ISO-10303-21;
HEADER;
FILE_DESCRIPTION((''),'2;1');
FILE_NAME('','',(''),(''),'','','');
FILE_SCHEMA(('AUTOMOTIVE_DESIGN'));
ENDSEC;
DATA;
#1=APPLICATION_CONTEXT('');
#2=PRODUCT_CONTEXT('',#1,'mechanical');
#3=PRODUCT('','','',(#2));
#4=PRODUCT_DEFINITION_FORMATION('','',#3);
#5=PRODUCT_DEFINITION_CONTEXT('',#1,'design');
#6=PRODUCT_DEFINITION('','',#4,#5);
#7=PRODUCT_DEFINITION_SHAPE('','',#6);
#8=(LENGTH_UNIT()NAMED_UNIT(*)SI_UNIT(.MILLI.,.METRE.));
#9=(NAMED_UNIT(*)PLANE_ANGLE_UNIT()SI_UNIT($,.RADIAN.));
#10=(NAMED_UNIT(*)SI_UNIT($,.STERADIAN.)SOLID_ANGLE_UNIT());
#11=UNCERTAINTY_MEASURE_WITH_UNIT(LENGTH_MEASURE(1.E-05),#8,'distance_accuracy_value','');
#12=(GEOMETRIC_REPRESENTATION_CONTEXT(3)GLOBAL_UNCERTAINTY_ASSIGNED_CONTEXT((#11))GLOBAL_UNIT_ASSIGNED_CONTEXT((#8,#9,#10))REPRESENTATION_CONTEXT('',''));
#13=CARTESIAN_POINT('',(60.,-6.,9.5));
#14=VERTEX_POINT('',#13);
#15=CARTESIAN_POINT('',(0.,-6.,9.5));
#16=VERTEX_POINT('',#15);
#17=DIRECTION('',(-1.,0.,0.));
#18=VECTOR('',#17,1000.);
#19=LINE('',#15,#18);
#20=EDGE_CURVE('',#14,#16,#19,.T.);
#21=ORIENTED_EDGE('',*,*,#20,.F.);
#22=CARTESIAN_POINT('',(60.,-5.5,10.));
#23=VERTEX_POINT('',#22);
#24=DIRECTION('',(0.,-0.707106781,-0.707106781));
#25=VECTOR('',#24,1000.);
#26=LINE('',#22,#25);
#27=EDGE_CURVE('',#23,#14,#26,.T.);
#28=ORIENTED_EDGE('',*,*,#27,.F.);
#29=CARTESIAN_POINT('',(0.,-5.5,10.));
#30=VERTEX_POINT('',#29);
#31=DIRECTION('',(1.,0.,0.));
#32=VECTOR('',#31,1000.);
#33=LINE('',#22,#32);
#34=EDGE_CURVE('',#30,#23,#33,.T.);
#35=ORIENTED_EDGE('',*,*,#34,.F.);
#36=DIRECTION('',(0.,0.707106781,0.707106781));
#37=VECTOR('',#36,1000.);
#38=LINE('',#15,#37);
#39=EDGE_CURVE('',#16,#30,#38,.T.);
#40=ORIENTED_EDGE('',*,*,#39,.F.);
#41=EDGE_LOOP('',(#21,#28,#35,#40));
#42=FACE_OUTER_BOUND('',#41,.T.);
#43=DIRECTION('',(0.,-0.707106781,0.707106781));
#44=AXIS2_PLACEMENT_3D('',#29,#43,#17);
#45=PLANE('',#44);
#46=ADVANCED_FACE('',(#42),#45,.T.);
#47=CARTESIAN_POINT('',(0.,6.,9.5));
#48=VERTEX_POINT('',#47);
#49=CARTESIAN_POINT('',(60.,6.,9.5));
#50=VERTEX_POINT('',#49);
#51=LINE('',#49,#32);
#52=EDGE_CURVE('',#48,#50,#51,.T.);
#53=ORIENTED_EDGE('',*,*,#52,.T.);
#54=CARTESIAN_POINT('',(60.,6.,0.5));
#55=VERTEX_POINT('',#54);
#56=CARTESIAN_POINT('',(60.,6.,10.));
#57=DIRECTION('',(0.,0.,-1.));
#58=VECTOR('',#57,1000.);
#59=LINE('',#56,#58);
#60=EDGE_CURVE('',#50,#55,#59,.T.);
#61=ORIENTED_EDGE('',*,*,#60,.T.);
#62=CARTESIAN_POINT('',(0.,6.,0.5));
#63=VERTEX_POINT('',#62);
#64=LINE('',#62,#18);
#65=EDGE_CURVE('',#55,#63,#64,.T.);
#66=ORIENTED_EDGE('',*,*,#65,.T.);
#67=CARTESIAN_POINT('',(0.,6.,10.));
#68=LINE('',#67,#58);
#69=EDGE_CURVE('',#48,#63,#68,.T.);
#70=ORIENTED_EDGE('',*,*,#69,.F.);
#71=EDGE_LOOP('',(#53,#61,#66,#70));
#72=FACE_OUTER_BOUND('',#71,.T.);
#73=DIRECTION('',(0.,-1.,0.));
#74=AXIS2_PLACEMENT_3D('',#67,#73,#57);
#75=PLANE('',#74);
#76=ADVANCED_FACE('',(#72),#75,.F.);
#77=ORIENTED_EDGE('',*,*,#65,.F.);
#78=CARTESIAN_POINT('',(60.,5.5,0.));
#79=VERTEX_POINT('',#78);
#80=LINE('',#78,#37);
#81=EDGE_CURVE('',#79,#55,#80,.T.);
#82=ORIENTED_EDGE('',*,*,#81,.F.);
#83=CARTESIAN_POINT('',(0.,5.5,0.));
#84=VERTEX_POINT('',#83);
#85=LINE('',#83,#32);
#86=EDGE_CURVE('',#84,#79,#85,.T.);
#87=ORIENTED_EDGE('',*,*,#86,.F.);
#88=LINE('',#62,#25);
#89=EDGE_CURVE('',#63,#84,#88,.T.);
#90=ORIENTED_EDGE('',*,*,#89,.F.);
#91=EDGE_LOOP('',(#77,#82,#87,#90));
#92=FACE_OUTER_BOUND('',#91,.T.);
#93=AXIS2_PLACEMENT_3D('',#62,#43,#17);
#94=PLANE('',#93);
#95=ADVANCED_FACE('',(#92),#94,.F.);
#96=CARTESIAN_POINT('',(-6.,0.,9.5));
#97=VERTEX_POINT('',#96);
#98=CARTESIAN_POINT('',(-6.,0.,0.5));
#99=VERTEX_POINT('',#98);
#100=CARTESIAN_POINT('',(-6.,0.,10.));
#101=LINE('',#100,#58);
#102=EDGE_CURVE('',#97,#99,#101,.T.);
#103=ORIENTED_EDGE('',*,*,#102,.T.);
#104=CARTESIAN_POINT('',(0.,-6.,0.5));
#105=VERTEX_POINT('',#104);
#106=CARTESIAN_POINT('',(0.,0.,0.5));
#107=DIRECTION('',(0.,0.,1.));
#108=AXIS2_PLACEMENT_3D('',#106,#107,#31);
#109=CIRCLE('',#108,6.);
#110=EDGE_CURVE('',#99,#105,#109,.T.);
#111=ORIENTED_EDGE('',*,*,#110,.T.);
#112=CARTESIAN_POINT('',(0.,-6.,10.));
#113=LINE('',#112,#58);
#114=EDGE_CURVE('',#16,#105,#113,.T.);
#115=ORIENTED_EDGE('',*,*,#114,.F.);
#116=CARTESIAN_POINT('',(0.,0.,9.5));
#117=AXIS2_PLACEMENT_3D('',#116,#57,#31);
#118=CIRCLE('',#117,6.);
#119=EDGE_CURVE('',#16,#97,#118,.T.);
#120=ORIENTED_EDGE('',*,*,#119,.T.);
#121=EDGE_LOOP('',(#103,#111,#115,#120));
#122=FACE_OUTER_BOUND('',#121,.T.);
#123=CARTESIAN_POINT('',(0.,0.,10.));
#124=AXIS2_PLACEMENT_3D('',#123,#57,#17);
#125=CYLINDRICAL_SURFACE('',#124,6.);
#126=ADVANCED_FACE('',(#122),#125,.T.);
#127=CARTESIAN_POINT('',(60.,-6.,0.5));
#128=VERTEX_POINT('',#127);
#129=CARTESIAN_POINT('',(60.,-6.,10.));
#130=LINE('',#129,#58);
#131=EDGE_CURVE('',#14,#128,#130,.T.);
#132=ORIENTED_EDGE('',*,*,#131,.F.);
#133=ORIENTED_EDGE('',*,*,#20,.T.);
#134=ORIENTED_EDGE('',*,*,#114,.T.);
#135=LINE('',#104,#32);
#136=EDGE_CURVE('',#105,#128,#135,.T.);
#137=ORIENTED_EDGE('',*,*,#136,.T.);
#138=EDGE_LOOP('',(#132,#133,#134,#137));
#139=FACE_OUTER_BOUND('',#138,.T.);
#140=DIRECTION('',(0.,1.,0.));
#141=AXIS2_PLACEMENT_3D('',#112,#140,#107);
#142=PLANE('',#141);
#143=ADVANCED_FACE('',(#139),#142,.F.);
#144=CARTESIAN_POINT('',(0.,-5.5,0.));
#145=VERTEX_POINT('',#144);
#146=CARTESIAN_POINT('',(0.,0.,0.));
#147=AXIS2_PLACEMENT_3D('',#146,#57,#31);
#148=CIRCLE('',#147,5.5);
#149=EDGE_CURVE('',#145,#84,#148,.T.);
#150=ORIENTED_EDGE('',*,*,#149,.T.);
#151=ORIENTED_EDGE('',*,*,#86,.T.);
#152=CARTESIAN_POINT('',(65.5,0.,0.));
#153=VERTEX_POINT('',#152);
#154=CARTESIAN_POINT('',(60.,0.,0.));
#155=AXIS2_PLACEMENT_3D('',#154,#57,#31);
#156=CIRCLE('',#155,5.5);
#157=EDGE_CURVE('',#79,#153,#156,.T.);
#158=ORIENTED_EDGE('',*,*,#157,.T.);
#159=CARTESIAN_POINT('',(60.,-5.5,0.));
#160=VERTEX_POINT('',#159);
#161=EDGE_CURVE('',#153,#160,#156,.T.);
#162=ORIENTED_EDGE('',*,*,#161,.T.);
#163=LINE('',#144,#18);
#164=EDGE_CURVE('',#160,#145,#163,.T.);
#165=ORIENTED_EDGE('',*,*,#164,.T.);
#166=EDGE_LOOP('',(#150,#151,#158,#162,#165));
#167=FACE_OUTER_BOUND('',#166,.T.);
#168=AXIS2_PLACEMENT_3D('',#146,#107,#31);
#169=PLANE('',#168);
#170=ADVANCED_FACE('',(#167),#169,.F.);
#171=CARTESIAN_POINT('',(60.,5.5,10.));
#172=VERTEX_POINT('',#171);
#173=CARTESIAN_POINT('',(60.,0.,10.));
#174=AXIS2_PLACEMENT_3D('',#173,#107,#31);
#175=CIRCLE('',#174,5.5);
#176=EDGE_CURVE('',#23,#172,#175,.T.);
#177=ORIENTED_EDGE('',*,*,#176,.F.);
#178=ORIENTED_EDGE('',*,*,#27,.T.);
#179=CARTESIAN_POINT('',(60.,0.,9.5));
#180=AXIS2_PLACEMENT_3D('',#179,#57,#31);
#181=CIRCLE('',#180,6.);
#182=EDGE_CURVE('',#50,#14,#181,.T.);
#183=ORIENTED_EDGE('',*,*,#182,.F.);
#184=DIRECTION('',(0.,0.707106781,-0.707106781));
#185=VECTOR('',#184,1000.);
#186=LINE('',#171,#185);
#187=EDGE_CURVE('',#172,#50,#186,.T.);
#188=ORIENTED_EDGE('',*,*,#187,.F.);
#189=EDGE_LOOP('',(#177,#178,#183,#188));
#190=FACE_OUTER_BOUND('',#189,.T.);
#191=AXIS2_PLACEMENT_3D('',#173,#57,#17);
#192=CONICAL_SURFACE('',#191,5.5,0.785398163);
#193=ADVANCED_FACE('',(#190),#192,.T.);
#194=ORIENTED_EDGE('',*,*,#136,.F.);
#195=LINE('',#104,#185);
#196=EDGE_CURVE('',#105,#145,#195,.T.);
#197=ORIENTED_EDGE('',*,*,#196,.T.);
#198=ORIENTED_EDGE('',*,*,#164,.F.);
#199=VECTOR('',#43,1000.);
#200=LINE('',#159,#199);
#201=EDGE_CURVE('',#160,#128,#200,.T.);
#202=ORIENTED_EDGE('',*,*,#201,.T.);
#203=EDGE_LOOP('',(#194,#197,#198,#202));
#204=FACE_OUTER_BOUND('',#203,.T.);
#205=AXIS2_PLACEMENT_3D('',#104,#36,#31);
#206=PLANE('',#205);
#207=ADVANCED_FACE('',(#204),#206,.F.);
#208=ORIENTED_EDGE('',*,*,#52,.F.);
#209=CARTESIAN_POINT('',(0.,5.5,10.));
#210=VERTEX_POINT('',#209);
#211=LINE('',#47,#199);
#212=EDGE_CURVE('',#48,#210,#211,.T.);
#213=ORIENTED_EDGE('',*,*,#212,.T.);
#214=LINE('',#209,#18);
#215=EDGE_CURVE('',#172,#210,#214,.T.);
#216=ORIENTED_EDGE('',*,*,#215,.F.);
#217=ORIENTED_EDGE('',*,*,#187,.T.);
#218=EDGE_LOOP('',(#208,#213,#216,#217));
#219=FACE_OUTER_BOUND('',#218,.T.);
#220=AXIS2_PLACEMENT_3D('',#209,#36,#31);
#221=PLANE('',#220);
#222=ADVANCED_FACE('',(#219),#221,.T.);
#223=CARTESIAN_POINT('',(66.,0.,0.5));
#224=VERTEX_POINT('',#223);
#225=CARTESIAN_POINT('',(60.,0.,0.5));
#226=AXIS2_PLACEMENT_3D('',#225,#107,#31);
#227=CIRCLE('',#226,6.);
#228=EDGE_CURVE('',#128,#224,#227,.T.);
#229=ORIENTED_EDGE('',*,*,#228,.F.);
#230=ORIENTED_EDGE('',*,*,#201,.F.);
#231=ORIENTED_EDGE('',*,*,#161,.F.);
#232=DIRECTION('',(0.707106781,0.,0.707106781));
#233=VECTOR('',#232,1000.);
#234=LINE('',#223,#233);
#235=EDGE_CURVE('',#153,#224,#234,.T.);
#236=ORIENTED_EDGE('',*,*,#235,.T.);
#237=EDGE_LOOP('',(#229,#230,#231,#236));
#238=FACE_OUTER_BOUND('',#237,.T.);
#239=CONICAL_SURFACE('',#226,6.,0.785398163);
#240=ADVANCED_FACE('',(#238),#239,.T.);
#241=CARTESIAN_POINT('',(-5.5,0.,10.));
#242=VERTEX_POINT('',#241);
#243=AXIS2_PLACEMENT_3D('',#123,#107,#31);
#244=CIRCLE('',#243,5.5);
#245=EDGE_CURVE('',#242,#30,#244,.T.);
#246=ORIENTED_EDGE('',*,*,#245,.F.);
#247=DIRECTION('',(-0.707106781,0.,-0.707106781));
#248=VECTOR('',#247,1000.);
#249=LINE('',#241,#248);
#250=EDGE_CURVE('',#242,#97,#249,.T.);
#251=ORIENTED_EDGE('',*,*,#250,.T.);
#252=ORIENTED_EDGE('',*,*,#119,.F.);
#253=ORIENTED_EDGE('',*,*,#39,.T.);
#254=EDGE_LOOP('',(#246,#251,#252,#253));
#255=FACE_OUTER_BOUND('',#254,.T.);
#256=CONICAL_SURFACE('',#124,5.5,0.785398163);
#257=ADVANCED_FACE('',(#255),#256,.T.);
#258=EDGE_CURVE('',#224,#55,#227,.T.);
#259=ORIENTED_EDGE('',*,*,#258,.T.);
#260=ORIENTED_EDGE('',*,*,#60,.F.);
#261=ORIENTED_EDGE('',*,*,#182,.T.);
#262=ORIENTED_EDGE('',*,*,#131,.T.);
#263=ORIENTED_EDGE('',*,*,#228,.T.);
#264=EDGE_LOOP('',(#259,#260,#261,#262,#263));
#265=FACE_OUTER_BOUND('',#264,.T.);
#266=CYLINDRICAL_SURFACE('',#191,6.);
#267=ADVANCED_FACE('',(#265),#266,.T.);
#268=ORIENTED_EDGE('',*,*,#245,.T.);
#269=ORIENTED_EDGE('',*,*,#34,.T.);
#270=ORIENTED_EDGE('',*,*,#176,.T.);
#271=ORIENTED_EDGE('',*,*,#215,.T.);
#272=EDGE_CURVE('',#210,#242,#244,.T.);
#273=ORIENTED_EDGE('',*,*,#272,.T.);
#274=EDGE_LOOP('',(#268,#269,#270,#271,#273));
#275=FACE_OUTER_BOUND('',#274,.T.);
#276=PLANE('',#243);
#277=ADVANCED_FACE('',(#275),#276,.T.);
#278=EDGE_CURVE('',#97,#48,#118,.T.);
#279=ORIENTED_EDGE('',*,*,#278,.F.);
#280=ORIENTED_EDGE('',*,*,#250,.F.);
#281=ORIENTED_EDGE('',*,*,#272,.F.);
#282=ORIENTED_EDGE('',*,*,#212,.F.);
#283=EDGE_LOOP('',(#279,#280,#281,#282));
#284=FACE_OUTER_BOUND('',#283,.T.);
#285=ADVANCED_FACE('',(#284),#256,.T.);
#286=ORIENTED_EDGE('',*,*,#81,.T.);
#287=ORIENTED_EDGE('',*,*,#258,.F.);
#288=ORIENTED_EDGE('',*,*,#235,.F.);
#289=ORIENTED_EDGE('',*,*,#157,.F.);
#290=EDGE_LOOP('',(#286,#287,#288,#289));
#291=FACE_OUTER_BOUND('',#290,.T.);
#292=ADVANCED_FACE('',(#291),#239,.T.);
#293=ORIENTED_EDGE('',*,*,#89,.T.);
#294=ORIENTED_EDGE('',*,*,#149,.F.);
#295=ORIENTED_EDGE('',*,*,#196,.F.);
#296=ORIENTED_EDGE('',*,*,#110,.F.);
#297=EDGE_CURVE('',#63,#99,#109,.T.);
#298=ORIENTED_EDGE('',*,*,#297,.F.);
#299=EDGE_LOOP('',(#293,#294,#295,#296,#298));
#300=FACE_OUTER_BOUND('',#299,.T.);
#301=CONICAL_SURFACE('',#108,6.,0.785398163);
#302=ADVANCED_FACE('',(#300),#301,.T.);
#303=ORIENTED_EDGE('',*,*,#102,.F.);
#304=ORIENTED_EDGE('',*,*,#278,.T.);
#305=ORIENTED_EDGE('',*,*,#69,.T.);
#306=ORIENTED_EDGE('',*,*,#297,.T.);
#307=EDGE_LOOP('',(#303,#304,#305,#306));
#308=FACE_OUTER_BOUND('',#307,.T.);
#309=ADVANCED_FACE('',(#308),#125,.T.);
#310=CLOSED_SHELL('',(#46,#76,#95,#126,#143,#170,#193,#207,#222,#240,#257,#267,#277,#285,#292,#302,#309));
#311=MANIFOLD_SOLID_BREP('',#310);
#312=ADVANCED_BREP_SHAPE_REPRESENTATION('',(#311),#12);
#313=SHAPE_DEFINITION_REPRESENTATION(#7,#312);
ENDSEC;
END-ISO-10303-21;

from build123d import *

# Parameters (mm, degrees)
BOSS_EXTRUDE1_DEPTH = 10
CHAMFER1_SIZE       = 0.5


with BuildPart() as part:
    # Sketch1 → Boss-Extrude1 (new body)
    with BuildSketch(Plane.XY):
        with BuildLine():
            Line((0, 6), (60, 6))
            ThreePointArc((60, 6), (66, 0), (60, -6))
            Line((60, -6), (0, -6))
            ThreePointArc((0, -6), (-6, 0), (0, 6))
        make_face()
    extrude(amount=BOSS_EXTRUDE1_DEPTH)

    # Chamfer1
    chamfer1_edges = [part.edges().sort_by_distance(p)[0] for p in [
        (66, 0, 10),
        (30, 6, 10),
        (-6, 0, 10),
        (30, 6, 0),
        (66, 0, 0),
        (30, -6, 0),
        (-6, 0, 0),
        (30, -6, 10),
    ]]
    chamfer(chamfer1_edges, length=CHAMFER1_SIZE)


solid = part.part
